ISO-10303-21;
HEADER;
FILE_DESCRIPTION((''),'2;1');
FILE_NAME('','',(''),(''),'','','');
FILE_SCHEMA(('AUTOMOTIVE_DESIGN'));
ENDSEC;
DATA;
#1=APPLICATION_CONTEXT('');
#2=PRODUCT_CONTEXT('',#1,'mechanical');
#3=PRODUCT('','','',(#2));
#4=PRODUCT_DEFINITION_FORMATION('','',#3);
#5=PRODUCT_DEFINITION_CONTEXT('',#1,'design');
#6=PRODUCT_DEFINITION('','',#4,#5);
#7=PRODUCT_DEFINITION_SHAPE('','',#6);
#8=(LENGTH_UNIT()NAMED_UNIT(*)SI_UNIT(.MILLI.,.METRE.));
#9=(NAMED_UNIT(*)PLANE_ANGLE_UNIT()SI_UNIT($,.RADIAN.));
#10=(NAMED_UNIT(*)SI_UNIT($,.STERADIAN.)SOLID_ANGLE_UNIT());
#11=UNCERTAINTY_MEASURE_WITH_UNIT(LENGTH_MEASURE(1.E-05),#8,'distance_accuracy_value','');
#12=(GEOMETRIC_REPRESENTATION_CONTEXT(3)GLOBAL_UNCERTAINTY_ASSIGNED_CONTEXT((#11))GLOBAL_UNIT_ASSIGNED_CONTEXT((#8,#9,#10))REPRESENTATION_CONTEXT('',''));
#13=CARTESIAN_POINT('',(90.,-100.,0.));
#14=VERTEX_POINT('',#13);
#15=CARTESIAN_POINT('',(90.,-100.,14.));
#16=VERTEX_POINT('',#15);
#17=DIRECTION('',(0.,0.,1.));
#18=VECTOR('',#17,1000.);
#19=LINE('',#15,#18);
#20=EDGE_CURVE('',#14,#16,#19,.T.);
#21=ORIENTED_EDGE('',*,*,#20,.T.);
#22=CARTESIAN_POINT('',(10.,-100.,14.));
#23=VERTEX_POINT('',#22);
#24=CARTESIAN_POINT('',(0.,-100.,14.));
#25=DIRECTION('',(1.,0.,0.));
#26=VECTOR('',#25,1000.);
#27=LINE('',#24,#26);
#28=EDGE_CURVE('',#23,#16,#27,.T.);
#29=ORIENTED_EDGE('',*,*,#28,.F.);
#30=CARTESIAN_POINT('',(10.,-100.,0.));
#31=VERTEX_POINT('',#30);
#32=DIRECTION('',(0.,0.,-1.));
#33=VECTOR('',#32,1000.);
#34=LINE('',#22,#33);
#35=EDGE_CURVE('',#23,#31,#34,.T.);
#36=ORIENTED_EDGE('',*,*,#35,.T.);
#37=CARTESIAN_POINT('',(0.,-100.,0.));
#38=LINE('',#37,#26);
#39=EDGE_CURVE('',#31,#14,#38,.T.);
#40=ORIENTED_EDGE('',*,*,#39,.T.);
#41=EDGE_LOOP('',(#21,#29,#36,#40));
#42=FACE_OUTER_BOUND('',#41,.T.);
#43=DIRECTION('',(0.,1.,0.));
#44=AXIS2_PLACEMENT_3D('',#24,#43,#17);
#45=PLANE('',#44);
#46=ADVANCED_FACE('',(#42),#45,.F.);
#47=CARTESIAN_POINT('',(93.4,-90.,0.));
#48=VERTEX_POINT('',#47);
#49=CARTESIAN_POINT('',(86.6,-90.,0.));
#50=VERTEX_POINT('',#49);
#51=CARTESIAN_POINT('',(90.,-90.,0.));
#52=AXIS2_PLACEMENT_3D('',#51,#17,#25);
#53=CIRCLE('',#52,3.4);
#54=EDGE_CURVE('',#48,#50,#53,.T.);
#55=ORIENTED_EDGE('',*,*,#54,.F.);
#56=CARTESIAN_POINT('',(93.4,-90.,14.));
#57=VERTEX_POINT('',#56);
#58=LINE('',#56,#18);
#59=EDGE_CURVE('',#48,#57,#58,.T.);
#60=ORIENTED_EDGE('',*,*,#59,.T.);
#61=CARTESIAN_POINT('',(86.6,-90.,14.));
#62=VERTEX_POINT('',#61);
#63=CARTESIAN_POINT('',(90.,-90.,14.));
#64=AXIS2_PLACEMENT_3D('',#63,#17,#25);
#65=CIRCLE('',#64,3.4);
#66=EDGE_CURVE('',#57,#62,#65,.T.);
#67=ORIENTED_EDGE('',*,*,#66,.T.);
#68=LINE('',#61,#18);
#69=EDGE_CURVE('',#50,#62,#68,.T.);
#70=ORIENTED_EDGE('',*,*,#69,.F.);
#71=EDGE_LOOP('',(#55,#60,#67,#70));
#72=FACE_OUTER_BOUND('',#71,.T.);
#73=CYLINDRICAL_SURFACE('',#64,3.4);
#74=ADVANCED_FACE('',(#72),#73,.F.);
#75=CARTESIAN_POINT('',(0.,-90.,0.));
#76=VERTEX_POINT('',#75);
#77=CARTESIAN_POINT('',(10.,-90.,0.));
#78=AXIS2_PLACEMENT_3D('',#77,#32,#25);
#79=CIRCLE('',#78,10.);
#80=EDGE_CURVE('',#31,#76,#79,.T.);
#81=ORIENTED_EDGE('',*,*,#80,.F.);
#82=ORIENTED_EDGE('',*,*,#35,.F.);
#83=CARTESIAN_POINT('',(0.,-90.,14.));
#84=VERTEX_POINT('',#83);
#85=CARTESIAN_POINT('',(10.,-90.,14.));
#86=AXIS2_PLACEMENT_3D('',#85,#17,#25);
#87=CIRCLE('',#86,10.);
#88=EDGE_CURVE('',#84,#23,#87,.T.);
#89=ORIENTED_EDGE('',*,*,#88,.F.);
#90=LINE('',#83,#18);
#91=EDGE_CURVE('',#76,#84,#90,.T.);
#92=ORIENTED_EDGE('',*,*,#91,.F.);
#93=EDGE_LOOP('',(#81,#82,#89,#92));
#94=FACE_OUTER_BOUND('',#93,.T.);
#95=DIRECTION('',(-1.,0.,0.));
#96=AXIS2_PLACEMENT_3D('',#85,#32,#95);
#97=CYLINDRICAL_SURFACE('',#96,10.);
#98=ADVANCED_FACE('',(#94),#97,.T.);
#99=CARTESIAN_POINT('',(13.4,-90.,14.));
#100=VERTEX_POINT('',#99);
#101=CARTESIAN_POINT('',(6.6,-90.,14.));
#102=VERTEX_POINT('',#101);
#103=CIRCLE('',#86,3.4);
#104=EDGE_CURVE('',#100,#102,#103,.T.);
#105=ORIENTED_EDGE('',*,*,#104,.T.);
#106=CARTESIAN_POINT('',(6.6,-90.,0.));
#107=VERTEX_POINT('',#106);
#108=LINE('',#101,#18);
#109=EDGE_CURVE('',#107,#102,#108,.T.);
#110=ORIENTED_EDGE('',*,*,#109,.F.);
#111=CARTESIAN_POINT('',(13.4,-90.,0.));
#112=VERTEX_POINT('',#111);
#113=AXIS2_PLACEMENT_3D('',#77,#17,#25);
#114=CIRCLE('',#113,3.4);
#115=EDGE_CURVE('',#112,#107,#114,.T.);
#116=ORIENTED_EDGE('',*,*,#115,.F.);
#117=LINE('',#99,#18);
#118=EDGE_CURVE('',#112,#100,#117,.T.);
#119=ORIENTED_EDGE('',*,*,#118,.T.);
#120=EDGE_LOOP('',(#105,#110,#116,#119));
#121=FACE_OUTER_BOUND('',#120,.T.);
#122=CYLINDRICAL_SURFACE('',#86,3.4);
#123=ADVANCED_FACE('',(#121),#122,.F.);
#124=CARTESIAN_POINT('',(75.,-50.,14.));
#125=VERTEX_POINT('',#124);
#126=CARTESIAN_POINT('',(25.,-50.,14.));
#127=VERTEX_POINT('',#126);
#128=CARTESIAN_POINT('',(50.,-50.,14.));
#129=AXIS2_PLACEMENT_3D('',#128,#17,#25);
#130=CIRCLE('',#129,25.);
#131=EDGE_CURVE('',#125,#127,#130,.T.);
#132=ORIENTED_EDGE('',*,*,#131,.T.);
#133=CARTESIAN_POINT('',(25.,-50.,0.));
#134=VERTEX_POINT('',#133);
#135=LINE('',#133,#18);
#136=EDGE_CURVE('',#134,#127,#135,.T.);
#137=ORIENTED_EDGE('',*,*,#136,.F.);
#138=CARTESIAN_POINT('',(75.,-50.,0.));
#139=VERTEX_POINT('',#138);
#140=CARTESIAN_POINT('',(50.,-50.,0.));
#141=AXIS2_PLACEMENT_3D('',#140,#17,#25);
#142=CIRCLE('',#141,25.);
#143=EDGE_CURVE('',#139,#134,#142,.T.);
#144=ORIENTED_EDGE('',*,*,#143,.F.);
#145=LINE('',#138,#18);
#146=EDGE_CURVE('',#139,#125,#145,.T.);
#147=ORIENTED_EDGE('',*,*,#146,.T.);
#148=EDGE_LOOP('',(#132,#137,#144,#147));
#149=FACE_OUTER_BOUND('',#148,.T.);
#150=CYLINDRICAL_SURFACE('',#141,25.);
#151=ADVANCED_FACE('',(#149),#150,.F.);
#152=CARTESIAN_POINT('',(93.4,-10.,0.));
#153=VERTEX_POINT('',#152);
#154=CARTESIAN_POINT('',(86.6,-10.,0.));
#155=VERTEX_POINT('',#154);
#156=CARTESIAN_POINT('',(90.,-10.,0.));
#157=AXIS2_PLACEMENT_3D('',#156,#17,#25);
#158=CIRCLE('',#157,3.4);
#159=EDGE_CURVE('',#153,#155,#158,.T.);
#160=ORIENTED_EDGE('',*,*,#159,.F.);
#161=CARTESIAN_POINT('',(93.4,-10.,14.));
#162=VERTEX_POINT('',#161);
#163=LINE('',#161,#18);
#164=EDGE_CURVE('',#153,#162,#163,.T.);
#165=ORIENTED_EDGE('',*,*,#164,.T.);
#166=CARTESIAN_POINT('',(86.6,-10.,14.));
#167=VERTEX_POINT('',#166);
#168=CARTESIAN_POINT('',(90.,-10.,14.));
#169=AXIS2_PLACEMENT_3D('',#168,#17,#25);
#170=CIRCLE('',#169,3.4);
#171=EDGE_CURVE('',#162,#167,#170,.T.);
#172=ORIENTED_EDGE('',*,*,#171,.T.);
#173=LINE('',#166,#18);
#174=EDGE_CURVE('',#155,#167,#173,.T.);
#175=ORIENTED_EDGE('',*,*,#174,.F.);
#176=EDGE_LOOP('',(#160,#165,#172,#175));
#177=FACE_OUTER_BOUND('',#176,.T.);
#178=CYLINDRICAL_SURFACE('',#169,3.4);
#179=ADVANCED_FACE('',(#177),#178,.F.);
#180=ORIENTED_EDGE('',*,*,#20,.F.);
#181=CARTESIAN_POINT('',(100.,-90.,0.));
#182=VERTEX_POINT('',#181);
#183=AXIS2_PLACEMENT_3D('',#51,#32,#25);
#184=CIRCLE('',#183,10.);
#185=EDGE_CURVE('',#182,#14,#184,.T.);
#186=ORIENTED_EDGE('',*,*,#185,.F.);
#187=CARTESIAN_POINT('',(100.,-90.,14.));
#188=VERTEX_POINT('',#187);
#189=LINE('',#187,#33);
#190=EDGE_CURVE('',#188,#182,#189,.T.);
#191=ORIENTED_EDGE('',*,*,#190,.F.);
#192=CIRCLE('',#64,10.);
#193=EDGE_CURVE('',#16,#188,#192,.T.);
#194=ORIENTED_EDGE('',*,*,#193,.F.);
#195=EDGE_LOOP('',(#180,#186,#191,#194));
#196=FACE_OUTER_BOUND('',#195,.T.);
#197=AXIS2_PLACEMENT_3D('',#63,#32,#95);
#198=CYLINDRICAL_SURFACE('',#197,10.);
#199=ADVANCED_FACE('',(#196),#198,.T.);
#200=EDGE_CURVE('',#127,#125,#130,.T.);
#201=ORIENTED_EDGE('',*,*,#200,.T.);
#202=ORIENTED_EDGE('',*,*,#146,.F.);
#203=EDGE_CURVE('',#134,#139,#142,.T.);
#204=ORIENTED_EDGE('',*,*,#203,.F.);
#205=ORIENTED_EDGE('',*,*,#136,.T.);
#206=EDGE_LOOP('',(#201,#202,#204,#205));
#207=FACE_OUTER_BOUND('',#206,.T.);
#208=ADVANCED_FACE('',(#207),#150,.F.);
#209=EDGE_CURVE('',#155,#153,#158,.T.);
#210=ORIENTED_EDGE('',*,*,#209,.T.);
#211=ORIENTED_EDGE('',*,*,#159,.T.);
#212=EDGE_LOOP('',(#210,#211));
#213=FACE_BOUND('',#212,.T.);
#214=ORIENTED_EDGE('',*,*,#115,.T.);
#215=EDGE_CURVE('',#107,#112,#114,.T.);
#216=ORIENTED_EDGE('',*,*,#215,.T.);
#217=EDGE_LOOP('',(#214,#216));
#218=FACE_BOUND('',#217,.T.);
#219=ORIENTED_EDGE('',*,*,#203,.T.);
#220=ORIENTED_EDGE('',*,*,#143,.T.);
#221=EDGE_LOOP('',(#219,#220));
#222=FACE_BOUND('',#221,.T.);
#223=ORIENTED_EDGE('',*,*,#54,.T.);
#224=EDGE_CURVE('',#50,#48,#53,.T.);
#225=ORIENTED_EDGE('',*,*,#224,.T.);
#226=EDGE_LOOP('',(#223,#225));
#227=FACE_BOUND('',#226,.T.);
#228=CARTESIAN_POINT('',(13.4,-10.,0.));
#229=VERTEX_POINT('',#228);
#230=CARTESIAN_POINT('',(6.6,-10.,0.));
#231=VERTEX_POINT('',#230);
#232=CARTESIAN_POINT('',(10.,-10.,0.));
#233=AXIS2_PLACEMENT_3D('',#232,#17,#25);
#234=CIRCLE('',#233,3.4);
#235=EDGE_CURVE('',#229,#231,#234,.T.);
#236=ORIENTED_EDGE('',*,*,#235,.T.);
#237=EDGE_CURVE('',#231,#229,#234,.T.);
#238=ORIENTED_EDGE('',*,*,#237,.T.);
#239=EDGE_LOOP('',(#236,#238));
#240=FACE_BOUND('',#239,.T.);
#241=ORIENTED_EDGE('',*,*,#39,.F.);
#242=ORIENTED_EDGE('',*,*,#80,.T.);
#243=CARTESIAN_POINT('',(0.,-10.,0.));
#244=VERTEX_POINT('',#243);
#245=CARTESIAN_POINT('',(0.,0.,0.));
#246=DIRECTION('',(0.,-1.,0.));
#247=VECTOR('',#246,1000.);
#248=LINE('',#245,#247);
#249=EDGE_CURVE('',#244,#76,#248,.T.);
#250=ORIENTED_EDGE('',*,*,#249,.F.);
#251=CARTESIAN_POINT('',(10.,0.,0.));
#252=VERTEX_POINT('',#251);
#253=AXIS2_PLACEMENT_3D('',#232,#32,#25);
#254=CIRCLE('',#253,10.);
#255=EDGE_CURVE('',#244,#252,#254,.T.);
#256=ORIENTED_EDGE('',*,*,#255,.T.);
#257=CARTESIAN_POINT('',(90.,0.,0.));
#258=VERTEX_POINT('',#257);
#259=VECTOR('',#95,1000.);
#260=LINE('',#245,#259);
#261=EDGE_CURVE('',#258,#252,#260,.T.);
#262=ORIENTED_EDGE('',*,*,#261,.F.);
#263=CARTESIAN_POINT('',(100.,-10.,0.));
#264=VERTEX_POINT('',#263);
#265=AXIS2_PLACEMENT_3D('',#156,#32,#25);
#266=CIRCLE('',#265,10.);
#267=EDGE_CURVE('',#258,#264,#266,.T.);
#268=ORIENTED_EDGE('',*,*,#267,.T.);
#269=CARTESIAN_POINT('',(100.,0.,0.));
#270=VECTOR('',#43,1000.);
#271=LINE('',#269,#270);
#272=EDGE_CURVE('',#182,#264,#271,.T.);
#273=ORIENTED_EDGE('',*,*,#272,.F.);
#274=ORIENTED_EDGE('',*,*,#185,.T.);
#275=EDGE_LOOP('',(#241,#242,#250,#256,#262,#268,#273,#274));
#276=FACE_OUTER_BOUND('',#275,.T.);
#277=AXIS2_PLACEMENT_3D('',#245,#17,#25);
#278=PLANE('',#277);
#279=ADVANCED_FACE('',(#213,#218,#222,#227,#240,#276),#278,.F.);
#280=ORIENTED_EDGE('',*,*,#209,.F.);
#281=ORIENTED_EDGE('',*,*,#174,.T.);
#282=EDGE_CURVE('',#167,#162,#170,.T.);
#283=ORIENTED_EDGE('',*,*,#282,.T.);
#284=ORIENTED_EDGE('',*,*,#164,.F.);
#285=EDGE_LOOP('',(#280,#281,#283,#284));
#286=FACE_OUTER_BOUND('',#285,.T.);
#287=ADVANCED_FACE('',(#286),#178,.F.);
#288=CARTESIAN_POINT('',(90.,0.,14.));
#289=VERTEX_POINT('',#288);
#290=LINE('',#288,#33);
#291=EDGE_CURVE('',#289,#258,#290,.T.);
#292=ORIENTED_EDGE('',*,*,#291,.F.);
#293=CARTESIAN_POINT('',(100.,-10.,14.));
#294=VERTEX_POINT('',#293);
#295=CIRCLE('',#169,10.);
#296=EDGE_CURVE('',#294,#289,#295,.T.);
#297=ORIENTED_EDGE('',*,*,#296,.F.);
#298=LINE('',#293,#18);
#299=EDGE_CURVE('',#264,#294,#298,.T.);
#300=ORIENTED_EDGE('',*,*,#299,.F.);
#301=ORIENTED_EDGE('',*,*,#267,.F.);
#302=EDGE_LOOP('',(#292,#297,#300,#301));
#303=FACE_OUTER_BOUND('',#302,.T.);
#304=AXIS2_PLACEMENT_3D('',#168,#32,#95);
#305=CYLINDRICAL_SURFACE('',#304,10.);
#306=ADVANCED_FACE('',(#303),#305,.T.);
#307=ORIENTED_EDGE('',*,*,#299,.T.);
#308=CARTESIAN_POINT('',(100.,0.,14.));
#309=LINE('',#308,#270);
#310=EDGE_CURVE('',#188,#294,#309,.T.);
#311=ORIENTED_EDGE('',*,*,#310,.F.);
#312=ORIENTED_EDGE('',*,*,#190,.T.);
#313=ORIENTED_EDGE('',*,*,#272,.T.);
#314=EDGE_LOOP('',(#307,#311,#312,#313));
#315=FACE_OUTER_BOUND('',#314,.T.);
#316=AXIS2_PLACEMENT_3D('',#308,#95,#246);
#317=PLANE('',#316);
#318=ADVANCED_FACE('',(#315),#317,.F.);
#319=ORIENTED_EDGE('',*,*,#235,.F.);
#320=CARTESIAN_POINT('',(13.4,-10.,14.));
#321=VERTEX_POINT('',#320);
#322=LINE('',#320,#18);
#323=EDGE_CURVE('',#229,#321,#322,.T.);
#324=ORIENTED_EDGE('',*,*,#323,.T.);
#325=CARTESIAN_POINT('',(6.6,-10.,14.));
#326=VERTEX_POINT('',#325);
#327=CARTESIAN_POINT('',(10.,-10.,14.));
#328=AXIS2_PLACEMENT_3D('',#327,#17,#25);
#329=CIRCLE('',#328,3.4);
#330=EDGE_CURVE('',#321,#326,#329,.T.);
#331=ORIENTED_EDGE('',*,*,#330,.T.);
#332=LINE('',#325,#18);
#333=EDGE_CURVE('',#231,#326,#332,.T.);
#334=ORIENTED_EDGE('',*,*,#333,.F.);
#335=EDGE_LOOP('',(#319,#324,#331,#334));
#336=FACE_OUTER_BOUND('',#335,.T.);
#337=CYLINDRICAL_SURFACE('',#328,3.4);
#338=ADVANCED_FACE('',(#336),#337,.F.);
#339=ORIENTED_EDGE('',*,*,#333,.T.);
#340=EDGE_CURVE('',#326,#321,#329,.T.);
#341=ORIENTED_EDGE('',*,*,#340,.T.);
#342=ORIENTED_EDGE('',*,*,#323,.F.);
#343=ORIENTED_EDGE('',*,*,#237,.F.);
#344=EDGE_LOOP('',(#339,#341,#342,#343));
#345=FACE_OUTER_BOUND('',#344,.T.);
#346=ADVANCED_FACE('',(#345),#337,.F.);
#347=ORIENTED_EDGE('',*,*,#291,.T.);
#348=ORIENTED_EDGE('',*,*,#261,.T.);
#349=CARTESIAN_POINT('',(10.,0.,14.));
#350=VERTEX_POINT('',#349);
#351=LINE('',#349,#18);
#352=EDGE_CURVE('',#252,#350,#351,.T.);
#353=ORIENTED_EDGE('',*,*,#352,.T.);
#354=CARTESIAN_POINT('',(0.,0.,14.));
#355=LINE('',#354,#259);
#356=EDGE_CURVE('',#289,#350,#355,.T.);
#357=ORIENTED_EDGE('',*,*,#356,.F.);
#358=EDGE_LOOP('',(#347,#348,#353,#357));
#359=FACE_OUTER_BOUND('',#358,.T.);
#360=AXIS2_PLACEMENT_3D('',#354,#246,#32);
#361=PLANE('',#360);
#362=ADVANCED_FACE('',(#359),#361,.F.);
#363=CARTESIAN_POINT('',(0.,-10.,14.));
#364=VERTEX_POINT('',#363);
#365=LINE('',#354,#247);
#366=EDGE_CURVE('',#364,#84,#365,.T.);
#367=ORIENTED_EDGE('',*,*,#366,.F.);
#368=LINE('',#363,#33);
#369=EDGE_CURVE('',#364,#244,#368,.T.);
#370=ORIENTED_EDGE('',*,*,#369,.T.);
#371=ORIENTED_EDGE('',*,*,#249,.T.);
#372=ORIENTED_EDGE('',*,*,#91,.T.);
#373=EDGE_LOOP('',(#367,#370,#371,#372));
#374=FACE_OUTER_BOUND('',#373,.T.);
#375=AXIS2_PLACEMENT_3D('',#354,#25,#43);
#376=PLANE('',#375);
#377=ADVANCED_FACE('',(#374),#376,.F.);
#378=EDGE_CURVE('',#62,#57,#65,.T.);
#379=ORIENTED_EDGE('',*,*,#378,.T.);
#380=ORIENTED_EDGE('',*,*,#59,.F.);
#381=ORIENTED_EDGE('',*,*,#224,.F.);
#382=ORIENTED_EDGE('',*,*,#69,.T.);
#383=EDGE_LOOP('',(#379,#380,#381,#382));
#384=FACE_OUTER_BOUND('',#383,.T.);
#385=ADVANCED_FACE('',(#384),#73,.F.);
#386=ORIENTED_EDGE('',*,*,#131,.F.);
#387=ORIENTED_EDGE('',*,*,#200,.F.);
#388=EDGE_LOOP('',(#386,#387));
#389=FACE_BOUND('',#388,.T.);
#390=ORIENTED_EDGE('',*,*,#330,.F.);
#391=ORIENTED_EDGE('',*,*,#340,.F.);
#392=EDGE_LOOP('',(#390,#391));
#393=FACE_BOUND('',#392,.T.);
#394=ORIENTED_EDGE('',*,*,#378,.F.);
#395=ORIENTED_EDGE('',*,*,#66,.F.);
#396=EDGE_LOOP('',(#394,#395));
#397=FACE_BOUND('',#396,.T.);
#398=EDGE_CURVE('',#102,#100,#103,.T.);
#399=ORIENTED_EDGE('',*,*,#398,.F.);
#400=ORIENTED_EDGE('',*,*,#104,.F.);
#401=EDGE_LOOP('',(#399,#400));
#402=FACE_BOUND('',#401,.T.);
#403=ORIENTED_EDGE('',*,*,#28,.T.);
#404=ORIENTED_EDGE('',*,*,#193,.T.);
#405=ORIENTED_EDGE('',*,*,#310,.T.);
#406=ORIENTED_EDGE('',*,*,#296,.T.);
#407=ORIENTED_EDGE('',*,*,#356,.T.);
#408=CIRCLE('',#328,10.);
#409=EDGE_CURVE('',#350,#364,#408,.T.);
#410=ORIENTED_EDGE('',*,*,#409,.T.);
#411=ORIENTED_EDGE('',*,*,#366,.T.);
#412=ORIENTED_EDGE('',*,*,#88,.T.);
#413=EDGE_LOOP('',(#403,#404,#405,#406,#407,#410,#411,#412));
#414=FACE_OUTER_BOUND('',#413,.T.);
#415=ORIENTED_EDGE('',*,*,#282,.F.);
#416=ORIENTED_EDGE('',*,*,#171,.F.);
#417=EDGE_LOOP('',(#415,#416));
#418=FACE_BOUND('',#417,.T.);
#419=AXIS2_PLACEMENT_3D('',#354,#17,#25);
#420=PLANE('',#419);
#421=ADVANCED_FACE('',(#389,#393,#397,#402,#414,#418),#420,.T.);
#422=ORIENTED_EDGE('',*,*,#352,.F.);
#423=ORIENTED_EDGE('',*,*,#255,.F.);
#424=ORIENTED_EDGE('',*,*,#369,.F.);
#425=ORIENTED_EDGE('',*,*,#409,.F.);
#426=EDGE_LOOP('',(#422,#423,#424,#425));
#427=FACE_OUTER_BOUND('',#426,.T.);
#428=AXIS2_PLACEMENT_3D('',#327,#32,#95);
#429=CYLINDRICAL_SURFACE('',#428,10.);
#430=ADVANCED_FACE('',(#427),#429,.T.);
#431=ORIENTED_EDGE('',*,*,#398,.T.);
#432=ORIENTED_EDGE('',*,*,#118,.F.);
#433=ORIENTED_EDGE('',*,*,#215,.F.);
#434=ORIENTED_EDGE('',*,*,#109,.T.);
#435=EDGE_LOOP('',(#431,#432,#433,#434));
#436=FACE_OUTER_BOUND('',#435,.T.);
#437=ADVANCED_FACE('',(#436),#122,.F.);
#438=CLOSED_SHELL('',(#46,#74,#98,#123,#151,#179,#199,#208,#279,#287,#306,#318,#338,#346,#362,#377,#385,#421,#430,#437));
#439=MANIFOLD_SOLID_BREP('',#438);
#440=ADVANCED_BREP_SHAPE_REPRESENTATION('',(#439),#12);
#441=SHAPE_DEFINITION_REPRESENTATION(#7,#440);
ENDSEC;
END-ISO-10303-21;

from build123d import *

# Parameters (mm, degrees)
SKETCH1_W           = 100
SKETCH1_H           = 100
BOSS_EXTRUDE1_DEPTH = 14
SKETCH2_R           = 25
CUT_EXTRUDE1_DEPTH  = 143.112631388
M8_TAPPED_HOLE1_D   = 6.8
FILLET1_R           = 10


with BuildPart() as part:
    # Sketch1 → Boss-Extrude1 (new body)
    with BuildSketch(Plane.XY):
        with Locations((50, -50)):
            Rectangle(SKETCH1_W, SKETCH1_H)
    extrude(amount=BOSS_EXTRUDE1_DEPTH)

    # Sketch2 → Cut-Extrude1 (cut, through all)
    with BuildSketch(Plane.XY.offset(14)):
        with Locations((50, -50)):
            Circle(SKETCH2_R)
    extrude(amount=-CUT_EXTRUDE1_DEPTH, mode=Mode.SUBTRACT)

    # M8 Tapped Hole1 (through all)
    with Locations(Plane.XY.offset(14)):
        with Locations((10, -10), (90, -10), (10, -90), (90, -90)):
            Hole(M8_TAPPED_HOLE1_D / 2)

    # Fillet1
    fillet1_edges = [part.edges().sort_by_distance(p)[0] for p in [
        (0, 0, 7),
        (100, 0, 7),
        (100, -100, 7),
        (0, -100, 7),
    ]]
    fillet(fillet1_edges, radius=FILLET1_R)


solid = part.part
